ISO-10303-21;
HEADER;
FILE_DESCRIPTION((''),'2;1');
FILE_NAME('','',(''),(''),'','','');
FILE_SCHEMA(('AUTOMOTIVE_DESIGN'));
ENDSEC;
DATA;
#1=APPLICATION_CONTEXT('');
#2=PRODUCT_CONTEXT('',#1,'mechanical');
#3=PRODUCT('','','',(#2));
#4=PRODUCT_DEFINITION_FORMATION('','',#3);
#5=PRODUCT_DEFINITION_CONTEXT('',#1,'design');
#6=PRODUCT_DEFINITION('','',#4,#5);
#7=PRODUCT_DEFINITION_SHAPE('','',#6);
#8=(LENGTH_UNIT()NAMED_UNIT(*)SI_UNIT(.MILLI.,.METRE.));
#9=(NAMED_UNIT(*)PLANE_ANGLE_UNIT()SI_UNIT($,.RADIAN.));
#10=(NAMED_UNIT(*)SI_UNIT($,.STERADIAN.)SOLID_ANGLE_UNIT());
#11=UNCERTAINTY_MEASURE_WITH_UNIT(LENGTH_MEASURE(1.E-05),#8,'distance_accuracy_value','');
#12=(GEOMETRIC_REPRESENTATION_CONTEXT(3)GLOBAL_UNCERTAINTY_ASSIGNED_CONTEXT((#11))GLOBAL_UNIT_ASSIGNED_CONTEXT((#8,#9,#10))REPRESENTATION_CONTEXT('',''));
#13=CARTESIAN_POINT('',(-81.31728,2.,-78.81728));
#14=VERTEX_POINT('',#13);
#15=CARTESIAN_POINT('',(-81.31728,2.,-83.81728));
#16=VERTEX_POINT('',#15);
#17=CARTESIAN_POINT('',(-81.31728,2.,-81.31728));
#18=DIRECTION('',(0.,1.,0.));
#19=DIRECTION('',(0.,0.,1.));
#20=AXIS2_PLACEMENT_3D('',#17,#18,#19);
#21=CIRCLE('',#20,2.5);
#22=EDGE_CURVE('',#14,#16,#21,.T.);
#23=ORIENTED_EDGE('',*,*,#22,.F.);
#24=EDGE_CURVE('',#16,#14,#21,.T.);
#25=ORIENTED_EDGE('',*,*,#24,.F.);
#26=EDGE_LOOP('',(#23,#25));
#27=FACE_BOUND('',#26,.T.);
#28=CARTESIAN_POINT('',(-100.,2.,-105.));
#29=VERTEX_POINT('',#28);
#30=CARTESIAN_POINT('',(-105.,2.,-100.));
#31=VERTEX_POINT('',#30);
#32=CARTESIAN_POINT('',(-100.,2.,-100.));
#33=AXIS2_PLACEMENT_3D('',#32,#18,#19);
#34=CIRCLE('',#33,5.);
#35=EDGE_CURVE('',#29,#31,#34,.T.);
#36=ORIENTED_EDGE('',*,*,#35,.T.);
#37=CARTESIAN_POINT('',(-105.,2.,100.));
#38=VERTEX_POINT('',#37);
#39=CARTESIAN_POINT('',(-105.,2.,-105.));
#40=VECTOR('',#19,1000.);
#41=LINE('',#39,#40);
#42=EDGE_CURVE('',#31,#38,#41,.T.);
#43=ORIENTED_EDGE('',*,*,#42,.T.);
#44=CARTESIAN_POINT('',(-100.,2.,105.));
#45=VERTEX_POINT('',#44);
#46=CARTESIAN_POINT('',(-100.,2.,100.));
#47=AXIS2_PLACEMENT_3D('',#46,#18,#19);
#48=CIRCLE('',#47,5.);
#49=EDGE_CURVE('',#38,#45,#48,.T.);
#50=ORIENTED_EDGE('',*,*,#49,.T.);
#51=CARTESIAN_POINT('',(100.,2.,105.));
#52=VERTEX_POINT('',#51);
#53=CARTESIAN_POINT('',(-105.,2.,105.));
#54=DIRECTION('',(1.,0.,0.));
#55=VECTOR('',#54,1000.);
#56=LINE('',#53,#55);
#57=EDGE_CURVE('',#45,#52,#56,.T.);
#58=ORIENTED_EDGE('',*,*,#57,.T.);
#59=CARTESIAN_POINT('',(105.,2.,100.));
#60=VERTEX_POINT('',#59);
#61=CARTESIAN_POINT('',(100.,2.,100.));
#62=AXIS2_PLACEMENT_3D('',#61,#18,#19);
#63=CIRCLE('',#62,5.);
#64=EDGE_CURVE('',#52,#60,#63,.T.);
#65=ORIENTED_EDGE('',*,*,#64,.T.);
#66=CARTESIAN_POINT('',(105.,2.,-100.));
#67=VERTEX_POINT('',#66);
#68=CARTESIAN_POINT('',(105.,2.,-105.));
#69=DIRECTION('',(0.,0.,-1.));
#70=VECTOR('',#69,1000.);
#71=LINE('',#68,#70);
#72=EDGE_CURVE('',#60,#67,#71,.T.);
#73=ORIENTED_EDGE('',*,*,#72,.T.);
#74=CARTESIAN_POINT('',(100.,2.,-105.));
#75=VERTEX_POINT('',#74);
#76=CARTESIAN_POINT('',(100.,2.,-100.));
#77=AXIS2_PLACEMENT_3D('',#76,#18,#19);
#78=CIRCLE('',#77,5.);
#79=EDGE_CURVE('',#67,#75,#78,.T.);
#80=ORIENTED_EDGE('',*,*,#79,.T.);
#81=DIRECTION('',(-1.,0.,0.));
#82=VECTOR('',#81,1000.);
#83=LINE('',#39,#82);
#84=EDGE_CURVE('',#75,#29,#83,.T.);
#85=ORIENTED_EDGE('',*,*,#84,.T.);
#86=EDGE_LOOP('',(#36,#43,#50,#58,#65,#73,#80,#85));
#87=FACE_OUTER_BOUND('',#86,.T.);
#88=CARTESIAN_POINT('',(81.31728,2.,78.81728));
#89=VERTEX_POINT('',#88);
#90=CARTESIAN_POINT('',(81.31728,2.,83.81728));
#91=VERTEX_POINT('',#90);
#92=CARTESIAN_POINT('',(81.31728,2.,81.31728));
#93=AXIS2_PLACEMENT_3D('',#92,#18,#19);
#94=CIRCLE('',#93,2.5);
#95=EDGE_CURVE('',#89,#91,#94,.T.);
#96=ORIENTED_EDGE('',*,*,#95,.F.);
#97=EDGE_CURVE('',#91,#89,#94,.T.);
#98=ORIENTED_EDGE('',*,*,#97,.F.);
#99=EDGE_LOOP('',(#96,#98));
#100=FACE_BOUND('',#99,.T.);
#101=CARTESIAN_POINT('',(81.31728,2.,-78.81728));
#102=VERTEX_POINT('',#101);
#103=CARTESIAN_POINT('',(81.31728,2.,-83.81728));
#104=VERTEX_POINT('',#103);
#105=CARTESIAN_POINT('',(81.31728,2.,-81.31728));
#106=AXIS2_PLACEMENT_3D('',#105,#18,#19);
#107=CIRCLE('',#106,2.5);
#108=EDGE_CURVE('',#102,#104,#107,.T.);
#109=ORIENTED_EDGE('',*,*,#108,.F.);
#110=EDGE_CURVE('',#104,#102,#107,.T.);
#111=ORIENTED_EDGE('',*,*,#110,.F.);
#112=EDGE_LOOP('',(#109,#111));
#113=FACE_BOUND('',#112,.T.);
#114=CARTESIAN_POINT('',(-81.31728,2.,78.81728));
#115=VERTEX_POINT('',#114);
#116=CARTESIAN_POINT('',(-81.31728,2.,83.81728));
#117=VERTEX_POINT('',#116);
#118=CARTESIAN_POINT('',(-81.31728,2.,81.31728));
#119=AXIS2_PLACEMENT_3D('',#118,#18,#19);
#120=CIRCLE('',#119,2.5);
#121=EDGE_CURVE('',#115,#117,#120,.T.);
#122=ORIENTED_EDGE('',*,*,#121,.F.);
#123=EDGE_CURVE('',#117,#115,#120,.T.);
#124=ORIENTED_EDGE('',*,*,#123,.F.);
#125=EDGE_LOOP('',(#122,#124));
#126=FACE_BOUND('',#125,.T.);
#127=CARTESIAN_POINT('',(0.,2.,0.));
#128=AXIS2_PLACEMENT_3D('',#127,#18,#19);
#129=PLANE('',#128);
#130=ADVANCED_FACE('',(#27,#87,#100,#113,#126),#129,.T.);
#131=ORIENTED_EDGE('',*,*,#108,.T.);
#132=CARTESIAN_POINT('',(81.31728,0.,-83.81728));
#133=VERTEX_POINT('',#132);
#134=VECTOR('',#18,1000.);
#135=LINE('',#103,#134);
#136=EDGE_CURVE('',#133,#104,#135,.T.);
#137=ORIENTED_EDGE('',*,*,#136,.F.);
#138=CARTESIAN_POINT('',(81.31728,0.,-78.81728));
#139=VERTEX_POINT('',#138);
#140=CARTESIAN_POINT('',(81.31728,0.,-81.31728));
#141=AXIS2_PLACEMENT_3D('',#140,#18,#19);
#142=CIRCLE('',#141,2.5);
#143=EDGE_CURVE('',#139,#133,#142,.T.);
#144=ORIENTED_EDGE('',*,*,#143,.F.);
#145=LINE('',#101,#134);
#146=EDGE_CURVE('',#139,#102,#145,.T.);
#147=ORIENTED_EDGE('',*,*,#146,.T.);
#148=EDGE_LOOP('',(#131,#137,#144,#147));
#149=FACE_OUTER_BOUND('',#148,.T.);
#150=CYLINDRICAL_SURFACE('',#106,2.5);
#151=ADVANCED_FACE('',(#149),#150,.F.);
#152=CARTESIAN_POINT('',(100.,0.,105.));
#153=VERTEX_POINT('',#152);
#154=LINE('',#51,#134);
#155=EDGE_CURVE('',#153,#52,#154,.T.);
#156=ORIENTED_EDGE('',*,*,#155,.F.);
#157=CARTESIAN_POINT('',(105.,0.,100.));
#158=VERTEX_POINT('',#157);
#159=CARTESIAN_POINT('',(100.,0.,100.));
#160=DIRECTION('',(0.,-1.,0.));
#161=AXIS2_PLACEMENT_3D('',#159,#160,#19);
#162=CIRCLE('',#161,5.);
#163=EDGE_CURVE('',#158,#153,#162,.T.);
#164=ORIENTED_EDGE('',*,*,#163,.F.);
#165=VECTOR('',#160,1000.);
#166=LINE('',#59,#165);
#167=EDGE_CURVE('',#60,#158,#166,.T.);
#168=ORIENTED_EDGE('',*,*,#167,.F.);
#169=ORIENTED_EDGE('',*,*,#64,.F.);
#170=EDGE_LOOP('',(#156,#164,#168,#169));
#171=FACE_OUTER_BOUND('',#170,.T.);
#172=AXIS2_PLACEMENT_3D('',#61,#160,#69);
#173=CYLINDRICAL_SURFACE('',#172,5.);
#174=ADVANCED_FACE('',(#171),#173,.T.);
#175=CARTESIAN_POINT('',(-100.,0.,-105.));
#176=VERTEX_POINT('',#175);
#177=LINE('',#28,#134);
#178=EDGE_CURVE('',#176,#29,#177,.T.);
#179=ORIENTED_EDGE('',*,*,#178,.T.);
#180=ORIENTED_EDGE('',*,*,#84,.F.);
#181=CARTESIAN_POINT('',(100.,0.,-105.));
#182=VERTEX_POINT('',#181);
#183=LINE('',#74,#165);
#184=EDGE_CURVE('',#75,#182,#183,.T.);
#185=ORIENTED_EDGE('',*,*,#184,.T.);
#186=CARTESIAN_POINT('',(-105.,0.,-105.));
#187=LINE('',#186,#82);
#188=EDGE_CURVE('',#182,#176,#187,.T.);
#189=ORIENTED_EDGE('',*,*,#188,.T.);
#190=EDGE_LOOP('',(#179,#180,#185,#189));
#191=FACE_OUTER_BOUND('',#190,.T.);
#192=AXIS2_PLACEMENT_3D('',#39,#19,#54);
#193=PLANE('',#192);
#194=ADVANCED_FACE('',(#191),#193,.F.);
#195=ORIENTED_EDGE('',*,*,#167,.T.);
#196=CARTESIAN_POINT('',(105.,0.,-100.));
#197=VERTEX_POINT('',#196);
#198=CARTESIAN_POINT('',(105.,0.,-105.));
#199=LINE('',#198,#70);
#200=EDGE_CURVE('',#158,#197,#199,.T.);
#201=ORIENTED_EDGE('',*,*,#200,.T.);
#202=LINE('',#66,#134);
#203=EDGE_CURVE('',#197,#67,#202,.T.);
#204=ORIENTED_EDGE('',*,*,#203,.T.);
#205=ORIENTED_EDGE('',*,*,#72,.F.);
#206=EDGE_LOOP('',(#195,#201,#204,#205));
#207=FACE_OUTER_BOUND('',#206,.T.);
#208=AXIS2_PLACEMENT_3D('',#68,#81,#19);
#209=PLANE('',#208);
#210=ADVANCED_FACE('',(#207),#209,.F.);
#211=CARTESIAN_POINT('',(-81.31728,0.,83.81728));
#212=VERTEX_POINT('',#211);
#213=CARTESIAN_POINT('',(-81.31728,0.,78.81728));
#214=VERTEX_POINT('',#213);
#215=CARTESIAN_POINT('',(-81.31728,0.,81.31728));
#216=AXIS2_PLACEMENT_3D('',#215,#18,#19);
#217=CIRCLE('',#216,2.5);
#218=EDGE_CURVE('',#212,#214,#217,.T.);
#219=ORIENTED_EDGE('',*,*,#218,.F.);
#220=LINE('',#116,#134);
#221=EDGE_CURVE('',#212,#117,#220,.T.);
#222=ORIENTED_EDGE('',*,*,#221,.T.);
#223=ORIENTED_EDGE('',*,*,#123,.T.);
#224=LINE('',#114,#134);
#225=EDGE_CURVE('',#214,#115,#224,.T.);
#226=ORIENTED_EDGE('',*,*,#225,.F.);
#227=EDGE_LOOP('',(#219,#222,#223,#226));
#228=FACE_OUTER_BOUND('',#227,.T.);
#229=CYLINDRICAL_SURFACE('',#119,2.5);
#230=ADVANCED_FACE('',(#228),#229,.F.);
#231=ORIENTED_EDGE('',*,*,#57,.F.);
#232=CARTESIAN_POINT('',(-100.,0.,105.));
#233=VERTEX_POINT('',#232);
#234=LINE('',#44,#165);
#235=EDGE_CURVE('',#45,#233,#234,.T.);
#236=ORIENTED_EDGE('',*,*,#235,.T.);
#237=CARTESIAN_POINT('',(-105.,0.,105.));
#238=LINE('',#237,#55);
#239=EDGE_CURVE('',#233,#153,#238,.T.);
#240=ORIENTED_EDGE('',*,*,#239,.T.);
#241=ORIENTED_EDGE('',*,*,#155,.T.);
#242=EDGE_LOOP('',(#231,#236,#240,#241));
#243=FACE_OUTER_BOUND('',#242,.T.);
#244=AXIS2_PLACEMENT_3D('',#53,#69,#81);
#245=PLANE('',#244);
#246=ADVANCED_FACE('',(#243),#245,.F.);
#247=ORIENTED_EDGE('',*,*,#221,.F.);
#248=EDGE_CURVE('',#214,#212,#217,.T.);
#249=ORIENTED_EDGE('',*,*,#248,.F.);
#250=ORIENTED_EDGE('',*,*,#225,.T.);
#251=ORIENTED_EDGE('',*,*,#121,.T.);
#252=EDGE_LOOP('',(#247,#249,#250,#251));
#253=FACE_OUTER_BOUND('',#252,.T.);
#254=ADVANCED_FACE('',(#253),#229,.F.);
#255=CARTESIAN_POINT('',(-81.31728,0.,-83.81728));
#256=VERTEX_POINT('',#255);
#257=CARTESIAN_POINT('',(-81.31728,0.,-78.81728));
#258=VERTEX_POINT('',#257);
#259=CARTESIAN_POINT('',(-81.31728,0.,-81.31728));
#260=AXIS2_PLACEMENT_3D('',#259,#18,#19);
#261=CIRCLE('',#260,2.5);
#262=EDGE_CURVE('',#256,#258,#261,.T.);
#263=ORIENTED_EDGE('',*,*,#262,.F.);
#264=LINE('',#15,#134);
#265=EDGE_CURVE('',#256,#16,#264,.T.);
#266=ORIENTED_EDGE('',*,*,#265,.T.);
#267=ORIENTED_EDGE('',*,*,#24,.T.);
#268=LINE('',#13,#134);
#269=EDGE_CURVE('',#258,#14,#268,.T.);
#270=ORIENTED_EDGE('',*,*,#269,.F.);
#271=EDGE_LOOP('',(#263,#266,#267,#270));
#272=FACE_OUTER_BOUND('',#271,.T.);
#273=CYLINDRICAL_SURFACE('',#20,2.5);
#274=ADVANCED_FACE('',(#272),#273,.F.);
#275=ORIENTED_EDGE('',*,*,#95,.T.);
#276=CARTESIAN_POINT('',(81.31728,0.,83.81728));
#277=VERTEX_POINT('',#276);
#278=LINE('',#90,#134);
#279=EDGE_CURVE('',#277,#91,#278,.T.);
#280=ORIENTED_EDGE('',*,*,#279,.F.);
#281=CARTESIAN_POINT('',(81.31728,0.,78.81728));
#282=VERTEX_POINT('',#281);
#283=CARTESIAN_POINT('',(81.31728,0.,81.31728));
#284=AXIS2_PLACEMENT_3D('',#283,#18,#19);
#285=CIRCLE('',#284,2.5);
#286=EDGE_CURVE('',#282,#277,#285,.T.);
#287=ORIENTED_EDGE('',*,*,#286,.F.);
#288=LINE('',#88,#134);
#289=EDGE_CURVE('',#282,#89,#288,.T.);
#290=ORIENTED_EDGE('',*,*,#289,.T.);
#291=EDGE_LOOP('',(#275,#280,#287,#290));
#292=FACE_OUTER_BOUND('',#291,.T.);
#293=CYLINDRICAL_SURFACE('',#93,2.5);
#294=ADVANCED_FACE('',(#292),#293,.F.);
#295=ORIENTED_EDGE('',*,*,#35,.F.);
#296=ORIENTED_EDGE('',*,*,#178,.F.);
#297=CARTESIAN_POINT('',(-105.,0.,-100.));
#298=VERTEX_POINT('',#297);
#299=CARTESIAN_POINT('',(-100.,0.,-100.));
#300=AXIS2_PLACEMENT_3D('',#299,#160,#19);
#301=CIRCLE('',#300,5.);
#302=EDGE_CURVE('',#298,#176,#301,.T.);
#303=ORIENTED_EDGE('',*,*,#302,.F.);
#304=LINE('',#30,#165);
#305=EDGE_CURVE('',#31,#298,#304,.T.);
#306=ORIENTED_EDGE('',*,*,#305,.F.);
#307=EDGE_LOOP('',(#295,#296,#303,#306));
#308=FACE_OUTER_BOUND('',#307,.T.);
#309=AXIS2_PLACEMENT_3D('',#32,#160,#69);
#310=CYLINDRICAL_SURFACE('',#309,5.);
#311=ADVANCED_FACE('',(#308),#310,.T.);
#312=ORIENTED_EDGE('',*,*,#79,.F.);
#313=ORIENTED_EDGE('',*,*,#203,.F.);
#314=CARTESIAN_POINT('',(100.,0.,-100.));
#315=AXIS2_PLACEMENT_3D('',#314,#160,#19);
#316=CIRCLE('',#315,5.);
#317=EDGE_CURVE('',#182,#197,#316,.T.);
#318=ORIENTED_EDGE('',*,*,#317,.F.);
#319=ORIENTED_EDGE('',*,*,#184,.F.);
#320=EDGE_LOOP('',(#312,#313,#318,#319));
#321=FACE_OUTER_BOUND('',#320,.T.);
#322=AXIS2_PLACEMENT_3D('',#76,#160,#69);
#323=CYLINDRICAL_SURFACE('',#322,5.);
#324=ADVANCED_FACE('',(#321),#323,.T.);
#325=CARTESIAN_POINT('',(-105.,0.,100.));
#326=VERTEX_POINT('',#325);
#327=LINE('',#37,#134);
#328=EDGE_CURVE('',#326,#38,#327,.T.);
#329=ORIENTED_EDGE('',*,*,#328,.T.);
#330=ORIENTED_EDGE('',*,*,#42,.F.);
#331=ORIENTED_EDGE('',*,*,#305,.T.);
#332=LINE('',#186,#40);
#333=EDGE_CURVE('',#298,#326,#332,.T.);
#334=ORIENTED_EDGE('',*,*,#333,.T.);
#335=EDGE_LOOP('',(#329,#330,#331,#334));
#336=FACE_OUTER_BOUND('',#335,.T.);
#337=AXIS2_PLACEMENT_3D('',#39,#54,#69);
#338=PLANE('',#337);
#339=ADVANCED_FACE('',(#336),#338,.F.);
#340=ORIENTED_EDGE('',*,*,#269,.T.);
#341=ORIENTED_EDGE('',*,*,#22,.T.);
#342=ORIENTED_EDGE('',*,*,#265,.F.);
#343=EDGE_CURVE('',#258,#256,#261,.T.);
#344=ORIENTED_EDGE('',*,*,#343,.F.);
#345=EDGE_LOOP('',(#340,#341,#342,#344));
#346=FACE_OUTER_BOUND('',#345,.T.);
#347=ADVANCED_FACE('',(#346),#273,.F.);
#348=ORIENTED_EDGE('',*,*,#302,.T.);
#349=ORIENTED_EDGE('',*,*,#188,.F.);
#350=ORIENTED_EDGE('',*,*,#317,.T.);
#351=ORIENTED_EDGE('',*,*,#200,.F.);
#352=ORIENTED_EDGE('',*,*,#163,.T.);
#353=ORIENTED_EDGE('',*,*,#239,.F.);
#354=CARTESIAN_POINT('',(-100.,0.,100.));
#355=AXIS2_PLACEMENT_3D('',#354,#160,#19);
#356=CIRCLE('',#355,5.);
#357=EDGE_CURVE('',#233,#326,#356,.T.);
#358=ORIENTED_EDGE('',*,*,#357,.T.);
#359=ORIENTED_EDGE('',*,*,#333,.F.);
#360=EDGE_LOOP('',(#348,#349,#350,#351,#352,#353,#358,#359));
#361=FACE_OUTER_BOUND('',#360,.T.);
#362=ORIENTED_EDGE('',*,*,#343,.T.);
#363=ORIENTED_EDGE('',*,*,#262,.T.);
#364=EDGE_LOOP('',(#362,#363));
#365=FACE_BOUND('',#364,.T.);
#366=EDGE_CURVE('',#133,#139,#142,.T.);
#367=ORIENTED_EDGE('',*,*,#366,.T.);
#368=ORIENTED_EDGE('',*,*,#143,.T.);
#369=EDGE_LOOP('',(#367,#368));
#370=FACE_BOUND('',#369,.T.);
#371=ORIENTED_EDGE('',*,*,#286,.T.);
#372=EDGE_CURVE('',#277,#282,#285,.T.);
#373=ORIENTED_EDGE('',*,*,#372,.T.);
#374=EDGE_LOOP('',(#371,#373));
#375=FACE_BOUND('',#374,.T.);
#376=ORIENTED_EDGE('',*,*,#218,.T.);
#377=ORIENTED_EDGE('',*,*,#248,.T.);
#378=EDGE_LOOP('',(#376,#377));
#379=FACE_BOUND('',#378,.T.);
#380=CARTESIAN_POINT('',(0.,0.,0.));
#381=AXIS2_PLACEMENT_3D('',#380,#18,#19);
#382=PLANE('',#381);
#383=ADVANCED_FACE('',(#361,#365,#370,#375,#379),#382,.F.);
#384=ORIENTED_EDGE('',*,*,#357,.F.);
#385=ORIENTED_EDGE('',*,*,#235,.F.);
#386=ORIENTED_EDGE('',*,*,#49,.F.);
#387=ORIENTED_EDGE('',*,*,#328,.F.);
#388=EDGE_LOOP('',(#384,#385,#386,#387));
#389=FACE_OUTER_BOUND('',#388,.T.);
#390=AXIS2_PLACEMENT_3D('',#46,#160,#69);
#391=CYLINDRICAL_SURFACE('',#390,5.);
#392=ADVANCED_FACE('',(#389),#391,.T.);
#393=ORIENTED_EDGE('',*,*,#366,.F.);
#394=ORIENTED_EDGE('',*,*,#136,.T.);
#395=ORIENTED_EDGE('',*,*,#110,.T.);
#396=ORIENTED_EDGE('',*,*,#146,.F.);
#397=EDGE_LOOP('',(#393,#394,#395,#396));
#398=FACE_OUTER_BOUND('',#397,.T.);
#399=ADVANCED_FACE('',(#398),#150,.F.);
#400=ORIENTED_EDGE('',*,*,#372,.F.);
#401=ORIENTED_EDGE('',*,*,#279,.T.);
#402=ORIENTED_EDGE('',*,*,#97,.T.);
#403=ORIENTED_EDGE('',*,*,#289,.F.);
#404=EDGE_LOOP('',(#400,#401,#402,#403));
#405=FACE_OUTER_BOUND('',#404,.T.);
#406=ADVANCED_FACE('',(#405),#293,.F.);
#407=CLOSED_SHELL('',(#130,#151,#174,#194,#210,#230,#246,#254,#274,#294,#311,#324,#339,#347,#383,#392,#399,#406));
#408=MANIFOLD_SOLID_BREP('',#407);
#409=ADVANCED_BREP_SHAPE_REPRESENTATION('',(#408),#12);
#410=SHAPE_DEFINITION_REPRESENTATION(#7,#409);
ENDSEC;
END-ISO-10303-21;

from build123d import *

# Parameters (mm, degrees)
SKETCH_1_W            = 210
SKETCH_1_H            = 210
EXTRUDE_1_DEPTH       = 2
HOLE_WIZARD_5_0_5_1_D = 5
FILLET_1_R            = 5


with BuildPart() as part:
    # 草图1 → 凸台-拉伸1 (new body)
    with BuildSketch(Plane(origin=(0, 0, 0), x_dir=(1, 0, 0), z_dir=(0, 1, 0))):
        Rectangle(SKETCH_1_W, SKETCH_1_H)
    extrude(amount=EXTRUDE_1_DEPTH)

    # Ø5.0 (5) 直径孔1 (through all)
    with Locations(Plane(origin=(0, 2, 0), x_dir=(1, 0, 0), z_dir=(0, 1, 0))):
        with Locations((-81.317279836, -81.317279836), (-81.317279836, 81.317279836), (81.317279836, 81.317279836), (81.317279836, -81.317279836)):
            Hole(HOLE_WIZARD_5_0_5_1_D / 2)

    # 圆角1
    fillet_1_edges = [part.edges().sort_by_distance(p)[0] for p in [
        (105, 1, 105),
        (-105, 1, 105),
        (-105, 1, -105),
        (105, 1, -105),
    ]]
    fillet(fillet_1_edges, radius=FILLET_1_R)


solid = part.part
